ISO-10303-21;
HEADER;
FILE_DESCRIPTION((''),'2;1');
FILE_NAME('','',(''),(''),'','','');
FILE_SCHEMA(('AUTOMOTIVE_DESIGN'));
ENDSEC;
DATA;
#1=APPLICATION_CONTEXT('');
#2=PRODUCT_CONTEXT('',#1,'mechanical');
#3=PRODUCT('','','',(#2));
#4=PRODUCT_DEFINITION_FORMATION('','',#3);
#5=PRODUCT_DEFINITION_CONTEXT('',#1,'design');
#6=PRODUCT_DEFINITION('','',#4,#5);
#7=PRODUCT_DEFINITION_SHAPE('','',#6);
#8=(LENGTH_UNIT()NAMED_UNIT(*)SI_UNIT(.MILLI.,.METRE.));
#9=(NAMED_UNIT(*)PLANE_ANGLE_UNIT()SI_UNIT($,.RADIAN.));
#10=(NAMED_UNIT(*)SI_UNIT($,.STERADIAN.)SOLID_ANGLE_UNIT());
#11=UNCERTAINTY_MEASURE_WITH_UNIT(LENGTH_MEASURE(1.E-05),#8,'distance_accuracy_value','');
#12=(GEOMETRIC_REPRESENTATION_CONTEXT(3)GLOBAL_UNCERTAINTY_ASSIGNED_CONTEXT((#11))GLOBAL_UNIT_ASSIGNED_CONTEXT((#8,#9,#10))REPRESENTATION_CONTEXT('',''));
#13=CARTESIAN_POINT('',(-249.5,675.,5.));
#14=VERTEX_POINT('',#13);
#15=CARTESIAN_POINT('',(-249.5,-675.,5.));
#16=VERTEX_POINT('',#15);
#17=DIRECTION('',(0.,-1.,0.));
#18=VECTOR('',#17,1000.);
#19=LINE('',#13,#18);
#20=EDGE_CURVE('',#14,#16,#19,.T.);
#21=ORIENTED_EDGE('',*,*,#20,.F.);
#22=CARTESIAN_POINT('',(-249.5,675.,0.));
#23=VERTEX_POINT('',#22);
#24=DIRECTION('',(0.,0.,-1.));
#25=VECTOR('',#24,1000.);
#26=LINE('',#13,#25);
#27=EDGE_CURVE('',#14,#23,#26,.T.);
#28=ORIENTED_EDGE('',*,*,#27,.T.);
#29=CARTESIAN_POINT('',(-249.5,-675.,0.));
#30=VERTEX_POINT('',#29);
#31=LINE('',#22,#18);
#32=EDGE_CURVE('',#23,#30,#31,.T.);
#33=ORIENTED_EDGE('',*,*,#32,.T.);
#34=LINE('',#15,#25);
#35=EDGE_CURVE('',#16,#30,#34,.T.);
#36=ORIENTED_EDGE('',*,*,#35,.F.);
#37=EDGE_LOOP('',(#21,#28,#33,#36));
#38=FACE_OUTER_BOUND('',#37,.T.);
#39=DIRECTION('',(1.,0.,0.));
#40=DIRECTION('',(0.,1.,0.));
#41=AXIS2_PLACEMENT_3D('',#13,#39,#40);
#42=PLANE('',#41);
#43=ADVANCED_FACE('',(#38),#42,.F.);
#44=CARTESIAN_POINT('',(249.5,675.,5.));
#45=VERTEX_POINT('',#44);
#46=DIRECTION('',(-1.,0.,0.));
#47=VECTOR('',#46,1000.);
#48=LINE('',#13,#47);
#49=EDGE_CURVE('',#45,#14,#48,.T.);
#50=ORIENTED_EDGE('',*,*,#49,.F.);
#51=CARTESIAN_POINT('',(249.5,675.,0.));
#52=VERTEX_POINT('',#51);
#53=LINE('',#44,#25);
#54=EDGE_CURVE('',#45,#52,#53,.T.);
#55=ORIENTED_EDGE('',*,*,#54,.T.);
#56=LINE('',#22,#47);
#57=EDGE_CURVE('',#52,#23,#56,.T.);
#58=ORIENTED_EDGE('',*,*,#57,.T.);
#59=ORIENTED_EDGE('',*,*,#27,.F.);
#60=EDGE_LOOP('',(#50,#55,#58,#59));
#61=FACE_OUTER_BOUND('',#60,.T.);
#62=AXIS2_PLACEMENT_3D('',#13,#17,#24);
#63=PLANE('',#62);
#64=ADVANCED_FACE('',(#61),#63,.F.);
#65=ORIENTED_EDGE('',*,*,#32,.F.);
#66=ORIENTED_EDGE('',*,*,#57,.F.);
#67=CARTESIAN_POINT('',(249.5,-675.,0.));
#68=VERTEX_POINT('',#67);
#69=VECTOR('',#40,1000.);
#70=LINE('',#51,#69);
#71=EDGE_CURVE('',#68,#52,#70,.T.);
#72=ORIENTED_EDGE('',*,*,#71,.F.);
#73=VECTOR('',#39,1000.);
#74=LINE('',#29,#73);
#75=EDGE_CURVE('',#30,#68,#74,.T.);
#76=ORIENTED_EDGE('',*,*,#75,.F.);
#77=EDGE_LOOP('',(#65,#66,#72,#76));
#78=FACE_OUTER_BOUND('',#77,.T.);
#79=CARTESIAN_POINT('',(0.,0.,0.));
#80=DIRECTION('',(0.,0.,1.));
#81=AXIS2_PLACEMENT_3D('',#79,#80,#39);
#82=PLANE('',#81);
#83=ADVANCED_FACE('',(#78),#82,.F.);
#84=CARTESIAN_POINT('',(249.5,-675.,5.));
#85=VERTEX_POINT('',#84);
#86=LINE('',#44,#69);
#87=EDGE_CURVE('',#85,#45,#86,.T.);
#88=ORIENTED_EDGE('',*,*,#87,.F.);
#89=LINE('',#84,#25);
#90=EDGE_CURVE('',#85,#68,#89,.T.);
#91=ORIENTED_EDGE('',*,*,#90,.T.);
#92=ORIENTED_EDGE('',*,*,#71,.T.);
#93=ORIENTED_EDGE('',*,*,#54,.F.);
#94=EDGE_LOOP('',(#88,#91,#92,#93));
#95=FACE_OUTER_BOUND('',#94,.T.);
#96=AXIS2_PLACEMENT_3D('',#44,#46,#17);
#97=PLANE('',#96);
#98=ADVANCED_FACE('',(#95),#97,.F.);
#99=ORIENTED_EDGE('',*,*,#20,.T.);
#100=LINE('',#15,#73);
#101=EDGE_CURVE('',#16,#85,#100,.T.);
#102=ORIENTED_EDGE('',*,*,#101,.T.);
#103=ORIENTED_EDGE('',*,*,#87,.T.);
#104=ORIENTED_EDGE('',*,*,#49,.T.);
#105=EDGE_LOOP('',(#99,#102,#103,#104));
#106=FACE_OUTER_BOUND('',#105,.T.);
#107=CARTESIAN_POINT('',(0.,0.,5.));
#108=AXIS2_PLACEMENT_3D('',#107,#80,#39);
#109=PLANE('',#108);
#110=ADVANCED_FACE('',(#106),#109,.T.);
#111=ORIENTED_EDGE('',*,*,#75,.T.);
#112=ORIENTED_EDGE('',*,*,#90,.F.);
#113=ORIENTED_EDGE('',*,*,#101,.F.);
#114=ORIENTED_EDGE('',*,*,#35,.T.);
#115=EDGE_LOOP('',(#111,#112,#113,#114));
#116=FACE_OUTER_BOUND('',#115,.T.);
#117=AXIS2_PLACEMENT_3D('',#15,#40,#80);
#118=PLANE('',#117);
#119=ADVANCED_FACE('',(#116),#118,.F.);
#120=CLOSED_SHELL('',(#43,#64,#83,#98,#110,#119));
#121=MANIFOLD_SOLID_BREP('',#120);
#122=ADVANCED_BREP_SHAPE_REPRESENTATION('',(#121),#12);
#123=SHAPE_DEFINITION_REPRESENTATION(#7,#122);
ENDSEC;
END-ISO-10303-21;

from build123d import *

# Parameters (mm, degrees)
SKETCH_1_W      = 499
SKETCH_1_H      = 1350
EXTRUDE_1_DEPTH = 5


with BuildPart() as part:
    # 草图1 → 凸台-拉伸1 (new body)
    with BuildSketch(Plane.XY):
        Rectangle(SKETCH_1_W, SKETCH_1_H)
    extrude(amount=EXTRUDE_1_DEPTH)


solid = part.part
